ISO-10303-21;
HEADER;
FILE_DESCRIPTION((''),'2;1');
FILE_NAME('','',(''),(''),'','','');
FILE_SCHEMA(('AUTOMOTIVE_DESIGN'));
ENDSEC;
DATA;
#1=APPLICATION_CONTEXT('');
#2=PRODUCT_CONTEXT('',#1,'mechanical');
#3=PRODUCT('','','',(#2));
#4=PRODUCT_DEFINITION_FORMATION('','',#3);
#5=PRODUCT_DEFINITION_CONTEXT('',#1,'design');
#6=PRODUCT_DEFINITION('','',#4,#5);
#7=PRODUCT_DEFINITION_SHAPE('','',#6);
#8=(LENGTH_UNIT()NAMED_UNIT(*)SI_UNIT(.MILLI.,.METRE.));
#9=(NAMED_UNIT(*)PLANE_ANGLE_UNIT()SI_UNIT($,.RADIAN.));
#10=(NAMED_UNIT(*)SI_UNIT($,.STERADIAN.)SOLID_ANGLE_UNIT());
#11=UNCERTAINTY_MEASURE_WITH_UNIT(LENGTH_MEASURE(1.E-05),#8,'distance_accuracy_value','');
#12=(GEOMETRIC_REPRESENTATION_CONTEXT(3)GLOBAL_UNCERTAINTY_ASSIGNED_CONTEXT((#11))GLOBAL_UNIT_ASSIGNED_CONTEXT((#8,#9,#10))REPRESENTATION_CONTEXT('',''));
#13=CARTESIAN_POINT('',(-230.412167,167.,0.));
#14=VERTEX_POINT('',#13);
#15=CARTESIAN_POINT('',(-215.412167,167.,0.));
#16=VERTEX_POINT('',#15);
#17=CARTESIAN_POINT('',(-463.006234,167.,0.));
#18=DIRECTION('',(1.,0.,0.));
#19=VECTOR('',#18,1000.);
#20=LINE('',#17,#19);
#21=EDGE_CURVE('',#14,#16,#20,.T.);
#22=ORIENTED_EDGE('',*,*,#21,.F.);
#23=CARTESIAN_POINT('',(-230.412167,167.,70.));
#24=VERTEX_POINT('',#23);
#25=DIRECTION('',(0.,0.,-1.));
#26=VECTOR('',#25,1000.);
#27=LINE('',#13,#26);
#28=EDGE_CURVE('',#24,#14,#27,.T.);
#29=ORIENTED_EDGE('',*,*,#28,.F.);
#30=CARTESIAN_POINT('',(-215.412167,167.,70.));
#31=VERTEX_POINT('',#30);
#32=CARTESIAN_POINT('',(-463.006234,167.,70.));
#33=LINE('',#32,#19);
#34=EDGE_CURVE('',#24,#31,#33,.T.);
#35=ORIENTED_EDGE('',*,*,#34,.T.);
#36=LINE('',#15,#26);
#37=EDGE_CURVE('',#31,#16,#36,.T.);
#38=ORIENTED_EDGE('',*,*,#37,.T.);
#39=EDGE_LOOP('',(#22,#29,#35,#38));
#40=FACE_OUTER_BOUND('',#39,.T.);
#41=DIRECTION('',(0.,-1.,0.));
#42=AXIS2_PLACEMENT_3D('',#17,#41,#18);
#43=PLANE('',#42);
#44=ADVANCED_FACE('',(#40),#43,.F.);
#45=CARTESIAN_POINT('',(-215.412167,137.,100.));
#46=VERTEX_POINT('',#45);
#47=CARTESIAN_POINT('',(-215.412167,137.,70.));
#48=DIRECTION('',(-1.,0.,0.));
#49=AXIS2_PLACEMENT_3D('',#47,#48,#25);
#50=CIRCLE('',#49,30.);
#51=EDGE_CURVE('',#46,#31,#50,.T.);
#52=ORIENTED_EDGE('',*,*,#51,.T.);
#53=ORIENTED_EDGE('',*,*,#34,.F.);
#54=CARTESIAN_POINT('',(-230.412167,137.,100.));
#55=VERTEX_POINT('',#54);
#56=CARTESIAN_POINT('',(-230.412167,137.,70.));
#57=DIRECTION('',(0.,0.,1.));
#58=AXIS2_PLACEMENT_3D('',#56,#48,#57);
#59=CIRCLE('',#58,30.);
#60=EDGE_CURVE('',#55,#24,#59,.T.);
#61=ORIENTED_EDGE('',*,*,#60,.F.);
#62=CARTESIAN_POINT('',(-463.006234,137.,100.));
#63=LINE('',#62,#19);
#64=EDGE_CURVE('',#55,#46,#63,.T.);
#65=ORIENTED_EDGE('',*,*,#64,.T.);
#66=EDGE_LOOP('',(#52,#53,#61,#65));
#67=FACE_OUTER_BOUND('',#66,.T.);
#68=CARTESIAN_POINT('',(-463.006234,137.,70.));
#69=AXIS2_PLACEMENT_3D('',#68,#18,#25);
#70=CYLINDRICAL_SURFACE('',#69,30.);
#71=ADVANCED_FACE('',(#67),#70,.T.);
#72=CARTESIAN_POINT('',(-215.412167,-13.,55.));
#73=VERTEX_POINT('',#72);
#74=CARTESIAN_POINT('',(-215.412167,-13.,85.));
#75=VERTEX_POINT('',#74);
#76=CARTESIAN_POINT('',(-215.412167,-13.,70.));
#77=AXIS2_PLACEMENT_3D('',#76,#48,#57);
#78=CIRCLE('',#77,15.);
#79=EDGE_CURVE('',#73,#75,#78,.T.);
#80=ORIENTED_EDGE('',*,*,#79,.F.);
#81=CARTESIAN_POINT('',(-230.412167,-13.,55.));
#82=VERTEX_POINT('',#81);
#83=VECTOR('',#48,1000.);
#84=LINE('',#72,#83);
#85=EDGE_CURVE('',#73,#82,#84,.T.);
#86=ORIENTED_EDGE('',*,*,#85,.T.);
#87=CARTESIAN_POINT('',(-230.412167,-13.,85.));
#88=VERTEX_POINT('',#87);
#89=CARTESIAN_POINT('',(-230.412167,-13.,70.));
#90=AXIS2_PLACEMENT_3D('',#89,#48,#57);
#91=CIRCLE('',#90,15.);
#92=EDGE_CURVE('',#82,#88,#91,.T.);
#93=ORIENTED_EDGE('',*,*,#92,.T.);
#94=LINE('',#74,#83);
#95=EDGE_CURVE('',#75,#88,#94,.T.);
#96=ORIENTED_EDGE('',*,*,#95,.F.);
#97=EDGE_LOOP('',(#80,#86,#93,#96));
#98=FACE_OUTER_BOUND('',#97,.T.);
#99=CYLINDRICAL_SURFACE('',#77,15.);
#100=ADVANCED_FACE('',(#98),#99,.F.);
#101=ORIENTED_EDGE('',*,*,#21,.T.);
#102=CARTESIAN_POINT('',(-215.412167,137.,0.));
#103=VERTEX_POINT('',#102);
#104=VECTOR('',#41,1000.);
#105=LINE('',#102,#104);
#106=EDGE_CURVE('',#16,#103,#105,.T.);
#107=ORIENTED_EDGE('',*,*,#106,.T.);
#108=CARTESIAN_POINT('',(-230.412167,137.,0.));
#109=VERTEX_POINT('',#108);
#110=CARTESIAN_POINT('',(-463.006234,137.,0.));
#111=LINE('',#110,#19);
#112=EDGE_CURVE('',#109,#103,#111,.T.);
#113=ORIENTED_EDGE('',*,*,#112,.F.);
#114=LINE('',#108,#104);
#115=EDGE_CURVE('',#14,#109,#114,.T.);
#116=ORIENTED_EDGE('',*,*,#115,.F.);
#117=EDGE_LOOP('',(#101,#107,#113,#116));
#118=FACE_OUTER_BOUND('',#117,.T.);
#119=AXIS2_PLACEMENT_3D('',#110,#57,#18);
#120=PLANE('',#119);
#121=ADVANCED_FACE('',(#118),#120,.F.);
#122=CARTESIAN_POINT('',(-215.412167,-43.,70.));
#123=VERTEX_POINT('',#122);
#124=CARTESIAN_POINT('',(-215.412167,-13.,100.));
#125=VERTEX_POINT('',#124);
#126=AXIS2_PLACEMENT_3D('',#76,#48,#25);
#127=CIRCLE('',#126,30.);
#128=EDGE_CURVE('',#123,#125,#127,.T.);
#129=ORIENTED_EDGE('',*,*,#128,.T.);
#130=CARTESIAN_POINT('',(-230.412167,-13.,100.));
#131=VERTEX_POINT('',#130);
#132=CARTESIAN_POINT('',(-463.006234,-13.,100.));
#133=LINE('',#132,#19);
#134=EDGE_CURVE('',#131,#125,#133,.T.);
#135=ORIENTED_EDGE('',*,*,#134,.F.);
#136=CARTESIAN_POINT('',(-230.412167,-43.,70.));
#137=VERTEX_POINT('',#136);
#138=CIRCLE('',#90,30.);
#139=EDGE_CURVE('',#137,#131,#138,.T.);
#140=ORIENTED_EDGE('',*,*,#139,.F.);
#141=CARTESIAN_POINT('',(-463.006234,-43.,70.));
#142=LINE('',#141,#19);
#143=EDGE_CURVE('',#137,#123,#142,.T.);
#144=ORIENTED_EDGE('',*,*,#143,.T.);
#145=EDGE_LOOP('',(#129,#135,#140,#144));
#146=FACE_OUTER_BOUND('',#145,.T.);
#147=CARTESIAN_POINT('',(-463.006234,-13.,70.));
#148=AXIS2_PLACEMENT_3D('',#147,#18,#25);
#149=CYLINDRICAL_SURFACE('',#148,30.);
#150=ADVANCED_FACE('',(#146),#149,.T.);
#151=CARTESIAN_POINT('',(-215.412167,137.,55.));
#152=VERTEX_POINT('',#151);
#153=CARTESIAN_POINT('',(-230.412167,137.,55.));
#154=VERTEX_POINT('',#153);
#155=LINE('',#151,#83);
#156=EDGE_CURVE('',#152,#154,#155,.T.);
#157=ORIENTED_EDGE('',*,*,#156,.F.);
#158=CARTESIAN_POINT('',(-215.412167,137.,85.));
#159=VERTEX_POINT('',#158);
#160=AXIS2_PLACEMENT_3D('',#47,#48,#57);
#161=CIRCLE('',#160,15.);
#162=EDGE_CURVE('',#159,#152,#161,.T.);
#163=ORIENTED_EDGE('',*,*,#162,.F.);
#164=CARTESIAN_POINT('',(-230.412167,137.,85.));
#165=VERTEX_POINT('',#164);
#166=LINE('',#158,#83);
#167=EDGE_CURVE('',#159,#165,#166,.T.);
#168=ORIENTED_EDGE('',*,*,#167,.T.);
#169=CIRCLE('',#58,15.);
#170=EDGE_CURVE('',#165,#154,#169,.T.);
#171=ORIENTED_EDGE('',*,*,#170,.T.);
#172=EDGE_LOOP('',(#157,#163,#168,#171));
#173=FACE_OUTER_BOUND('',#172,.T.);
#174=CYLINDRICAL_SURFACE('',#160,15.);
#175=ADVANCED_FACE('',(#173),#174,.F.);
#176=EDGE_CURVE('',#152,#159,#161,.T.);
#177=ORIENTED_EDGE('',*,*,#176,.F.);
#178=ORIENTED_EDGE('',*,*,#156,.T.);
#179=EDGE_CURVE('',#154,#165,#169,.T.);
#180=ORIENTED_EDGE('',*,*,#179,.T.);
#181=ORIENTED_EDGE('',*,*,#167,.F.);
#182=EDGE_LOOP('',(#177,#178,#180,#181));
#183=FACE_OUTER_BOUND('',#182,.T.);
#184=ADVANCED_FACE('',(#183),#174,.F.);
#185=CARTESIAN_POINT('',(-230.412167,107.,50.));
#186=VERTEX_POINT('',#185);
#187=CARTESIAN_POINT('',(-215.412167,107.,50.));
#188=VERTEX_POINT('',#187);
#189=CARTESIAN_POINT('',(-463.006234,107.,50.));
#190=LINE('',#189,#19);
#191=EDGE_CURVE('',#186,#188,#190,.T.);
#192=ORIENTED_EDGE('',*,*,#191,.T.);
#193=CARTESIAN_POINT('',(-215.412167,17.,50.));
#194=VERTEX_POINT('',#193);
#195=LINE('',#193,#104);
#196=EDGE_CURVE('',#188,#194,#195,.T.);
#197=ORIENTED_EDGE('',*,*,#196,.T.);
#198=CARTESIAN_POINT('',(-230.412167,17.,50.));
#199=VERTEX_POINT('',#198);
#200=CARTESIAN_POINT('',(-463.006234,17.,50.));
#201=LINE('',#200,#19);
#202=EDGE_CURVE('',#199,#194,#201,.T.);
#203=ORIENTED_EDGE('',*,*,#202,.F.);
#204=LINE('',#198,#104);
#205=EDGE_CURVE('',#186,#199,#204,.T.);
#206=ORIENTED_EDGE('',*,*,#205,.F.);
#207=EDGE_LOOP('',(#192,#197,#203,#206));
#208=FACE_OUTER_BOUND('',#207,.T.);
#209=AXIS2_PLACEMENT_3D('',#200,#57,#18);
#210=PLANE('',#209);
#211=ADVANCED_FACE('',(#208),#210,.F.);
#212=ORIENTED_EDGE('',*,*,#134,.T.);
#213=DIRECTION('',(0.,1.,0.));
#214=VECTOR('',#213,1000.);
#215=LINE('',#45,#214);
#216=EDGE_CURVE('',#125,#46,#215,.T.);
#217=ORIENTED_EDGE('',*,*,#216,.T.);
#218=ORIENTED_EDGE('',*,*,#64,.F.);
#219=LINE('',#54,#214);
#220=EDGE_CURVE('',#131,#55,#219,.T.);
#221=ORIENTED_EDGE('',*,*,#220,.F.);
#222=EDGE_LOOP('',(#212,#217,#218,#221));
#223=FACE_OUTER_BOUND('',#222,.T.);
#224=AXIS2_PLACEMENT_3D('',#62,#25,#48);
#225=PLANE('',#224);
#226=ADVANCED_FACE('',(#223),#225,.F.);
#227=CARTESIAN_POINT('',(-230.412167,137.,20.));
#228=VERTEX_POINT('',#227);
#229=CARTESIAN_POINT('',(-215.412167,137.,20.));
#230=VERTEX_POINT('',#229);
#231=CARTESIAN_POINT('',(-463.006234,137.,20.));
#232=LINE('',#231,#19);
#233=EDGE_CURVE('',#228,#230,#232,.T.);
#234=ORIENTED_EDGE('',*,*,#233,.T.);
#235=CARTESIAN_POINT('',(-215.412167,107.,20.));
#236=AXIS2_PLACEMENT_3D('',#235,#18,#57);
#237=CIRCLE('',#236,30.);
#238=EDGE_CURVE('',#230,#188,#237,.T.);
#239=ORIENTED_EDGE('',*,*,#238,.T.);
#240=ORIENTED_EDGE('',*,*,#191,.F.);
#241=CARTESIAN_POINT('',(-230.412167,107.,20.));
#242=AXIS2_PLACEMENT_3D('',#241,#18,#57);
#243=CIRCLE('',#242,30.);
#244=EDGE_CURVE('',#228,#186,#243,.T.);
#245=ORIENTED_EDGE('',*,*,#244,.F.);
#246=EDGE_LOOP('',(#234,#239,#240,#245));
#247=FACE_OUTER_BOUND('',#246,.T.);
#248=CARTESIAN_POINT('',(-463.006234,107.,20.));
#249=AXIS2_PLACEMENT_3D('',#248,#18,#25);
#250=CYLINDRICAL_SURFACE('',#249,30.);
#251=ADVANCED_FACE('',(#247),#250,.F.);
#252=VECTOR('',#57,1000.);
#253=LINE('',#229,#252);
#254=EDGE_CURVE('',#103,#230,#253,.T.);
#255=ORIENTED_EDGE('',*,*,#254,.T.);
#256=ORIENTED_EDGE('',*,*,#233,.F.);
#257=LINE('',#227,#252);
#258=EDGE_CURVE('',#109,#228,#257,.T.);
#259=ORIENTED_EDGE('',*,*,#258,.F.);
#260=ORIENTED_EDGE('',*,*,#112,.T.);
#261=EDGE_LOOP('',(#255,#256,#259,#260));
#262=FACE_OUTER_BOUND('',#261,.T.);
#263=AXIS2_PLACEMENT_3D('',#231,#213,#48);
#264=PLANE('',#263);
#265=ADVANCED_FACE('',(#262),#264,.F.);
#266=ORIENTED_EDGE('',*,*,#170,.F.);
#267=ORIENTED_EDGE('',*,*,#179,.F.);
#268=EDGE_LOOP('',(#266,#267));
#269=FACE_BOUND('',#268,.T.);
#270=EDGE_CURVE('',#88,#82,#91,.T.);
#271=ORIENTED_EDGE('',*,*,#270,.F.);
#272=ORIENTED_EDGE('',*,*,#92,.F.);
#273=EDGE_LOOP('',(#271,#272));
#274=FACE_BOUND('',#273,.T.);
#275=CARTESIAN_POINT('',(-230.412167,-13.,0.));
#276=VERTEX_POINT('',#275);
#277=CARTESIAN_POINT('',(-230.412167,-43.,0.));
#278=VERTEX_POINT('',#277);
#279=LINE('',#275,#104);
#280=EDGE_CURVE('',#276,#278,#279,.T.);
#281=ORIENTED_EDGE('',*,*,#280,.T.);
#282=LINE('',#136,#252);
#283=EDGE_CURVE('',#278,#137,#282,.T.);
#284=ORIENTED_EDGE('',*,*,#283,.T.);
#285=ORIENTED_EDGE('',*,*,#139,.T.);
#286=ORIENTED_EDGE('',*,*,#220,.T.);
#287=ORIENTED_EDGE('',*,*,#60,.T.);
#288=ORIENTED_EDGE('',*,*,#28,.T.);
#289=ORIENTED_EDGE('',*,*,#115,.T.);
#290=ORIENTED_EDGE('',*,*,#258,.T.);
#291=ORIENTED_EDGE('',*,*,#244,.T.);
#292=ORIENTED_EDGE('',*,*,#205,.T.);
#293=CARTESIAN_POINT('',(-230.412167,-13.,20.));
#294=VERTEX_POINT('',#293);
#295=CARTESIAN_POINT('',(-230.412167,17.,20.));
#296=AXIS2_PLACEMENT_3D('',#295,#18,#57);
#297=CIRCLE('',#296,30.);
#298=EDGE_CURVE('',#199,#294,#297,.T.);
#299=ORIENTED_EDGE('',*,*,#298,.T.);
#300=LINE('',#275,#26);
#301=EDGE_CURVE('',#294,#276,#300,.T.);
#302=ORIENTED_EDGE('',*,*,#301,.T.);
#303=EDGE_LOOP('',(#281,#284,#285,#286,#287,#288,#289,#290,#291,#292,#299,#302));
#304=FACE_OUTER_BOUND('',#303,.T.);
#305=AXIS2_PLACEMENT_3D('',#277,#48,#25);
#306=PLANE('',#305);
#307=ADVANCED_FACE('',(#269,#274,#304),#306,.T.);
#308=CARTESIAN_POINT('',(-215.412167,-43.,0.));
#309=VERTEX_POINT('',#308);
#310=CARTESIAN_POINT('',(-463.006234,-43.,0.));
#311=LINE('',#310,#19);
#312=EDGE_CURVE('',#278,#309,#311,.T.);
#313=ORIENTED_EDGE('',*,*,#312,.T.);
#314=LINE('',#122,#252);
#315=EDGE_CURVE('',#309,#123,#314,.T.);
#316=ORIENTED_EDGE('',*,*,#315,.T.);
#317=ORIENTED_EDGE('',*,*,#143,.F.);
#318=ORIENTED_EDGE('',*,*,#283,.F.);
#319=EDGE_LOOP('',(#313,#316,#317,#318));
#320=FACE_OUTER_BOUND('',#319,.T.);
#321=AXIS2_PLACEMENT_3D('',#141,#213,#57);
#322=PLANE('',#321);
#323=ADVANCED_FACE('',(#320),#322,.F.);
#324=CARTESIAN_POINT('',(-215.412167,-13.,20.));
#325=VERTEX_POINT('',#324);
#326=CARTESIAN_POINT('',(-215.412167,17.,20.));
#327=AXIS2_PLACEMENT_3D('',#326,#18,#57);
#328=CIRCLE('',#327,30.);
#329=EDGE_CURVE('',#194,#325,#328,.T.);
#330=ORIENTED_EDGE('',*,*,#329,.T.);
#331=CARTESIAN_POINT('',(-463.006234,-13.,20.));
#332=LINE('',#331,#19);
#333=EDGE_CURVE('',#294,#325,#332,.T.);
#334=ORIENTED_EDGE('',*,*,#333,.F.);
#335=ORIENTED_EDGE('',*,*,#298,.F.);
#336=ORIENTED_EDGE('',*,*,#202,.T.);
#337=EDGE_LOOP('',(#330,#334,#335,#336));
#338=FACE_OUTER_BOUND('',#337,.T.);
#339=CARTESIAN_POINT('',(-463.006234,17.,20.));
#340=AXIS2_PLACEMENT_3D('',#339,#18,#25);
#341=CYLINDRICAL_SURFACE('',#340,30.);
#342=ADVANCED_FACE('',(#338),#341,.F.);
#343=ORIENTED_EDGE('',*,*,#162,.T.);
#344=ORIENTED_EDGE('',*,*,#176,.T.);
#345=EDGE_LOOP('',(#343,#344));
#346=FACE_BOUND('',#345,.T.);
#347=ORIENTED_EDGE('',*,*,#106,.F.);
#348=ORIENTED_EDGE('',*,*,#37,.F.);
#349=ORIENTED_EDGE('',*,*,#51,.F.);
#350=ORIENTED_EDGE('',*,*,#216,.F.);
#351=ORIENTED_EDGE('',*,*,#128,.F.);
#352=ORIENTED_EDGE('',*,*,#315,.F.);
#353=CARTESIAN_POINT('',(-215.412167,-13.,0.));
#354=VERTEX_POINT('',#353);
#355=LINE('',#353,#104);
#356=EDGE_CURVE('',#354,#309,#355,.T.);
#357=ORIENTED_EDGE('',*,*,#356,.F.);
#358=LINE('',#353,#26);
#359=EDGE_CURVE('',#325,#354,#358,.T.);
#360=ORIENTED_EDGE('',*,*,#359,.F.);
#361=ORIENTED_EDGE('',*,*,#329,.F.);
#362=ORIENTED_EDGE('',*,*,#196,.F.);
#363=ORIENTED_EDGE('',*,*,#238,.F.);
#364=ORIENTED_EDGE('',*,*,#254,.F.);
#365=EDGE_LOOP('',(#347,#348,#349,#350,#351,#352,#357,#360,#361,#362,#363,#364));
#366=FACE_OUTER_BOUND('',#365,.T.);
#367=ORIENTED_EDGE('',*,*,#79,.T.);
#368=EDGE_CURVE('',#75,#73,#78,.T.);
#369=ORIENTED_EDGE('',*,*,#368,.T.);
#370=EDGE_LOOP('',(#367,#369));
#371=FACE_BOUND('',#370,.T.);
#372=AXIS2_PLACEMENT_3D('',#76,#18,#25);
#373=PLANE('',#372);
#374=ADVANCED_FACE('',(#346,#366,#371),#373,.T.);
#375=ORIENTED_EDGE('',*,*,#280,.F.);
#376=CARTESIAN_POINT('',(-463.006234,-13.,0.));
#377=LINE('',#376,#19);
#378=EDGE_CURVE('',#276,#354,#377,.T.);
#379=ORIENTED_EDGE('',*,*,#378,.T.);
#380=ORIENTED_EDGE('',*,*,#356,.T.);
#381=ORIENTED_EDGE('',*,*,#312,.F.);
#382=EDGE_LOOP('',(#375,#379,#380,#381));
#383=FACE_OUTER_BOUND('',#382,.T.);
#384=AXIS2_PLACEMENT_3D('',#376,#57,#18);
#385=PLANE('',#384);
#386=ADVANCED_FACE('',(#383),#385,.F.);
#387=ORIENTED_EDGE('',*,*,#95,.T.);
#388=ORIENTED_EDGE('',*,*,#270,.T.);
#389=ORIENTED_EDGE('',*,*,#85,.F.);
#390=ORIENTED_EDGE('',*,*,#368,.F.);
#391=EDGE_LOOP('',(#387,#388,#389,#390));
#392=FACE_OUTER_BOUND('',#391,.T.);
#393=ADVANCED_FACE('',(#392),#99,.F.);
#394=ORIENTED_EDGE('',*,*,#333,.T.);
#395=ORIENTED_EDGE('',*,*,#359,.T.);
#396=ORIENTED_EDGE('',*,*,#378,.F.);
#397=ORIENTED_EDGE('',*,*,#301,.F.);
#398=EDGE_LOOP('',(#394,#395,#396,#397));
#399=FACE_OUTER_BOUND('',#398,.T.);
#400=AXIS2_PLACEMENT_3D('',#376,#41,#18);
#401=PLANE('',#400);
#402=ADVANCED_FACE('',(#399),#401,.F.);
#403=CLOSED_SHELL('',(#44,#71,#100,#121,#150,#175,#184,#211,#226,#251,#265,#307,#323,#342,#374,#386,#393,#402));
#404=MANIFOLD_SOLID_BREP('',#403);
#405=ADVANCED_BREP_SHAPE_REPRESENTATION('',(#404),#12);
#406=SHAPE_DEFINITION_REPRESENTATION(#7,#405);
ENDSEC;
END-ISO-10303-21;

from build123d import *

# Parameters (mm, degrees)
BOSS_EXTRUDE1_DEPTH     = 15
CUT_EXTRUDE1_DEPTH      = 196.228071752
CUT_EXTRUDE1_DEPTH_BACK = 196.228071752
SKETCH3_R               = 15


with BuildPart() as part:
    # Sketch2 → Boss-Extrude1 (new body)
    with BuildSketch(Plane.ZY.offset(215.412167325)):
        with BuildLine():
            Line((0, -13), (20, -13))
            ThreePointArc((20, -13), (41.213203436, -4.213203436), (50, 17))
            Line((50, 17), (50, 107))
            ThreePointArc((50, 107), (41.213203436, 128.213203436), (20, 137))
            Line((20, 137), (0, 137))
            Line((0, 137), (0, 167))
            Line((0, 167), (70, 167))
            ThreePointArc((70, 167), (91.213203436, 158.213203436), (100, 137))
            Line((100, 137), (100, -13))
            ThreePointArc((100, -13), (91.213203436, -34.213203436), (70, -43))
            Line((70, -43), (0, -43))
            Line((0, -43), (0, -13))
        make_face()
    extrude(amount=BOSS_EXTRUDE1_DEPTH)

    # Sketch3 → Cut-Extrude1 (cut, two sides: drawn at the far end of the back side and taken through both)
    with BuildSketch(Plane.ZY.offset(230.412167325).offset(-CUT_EXTRUDE1_DEPTH_BACK)):
        with Locations((70, -13)):
            Circle(SKETCH3_R)
        with Locations((70, 137)):
            Circle(SKETCH3_R)
    extrude(amount=CUT_EXTRUDE1_DEPTH + CUT_EXTRUDE1_DEPTH_BACK, mode=Mode.SUBTRACT)


solid = part.part
